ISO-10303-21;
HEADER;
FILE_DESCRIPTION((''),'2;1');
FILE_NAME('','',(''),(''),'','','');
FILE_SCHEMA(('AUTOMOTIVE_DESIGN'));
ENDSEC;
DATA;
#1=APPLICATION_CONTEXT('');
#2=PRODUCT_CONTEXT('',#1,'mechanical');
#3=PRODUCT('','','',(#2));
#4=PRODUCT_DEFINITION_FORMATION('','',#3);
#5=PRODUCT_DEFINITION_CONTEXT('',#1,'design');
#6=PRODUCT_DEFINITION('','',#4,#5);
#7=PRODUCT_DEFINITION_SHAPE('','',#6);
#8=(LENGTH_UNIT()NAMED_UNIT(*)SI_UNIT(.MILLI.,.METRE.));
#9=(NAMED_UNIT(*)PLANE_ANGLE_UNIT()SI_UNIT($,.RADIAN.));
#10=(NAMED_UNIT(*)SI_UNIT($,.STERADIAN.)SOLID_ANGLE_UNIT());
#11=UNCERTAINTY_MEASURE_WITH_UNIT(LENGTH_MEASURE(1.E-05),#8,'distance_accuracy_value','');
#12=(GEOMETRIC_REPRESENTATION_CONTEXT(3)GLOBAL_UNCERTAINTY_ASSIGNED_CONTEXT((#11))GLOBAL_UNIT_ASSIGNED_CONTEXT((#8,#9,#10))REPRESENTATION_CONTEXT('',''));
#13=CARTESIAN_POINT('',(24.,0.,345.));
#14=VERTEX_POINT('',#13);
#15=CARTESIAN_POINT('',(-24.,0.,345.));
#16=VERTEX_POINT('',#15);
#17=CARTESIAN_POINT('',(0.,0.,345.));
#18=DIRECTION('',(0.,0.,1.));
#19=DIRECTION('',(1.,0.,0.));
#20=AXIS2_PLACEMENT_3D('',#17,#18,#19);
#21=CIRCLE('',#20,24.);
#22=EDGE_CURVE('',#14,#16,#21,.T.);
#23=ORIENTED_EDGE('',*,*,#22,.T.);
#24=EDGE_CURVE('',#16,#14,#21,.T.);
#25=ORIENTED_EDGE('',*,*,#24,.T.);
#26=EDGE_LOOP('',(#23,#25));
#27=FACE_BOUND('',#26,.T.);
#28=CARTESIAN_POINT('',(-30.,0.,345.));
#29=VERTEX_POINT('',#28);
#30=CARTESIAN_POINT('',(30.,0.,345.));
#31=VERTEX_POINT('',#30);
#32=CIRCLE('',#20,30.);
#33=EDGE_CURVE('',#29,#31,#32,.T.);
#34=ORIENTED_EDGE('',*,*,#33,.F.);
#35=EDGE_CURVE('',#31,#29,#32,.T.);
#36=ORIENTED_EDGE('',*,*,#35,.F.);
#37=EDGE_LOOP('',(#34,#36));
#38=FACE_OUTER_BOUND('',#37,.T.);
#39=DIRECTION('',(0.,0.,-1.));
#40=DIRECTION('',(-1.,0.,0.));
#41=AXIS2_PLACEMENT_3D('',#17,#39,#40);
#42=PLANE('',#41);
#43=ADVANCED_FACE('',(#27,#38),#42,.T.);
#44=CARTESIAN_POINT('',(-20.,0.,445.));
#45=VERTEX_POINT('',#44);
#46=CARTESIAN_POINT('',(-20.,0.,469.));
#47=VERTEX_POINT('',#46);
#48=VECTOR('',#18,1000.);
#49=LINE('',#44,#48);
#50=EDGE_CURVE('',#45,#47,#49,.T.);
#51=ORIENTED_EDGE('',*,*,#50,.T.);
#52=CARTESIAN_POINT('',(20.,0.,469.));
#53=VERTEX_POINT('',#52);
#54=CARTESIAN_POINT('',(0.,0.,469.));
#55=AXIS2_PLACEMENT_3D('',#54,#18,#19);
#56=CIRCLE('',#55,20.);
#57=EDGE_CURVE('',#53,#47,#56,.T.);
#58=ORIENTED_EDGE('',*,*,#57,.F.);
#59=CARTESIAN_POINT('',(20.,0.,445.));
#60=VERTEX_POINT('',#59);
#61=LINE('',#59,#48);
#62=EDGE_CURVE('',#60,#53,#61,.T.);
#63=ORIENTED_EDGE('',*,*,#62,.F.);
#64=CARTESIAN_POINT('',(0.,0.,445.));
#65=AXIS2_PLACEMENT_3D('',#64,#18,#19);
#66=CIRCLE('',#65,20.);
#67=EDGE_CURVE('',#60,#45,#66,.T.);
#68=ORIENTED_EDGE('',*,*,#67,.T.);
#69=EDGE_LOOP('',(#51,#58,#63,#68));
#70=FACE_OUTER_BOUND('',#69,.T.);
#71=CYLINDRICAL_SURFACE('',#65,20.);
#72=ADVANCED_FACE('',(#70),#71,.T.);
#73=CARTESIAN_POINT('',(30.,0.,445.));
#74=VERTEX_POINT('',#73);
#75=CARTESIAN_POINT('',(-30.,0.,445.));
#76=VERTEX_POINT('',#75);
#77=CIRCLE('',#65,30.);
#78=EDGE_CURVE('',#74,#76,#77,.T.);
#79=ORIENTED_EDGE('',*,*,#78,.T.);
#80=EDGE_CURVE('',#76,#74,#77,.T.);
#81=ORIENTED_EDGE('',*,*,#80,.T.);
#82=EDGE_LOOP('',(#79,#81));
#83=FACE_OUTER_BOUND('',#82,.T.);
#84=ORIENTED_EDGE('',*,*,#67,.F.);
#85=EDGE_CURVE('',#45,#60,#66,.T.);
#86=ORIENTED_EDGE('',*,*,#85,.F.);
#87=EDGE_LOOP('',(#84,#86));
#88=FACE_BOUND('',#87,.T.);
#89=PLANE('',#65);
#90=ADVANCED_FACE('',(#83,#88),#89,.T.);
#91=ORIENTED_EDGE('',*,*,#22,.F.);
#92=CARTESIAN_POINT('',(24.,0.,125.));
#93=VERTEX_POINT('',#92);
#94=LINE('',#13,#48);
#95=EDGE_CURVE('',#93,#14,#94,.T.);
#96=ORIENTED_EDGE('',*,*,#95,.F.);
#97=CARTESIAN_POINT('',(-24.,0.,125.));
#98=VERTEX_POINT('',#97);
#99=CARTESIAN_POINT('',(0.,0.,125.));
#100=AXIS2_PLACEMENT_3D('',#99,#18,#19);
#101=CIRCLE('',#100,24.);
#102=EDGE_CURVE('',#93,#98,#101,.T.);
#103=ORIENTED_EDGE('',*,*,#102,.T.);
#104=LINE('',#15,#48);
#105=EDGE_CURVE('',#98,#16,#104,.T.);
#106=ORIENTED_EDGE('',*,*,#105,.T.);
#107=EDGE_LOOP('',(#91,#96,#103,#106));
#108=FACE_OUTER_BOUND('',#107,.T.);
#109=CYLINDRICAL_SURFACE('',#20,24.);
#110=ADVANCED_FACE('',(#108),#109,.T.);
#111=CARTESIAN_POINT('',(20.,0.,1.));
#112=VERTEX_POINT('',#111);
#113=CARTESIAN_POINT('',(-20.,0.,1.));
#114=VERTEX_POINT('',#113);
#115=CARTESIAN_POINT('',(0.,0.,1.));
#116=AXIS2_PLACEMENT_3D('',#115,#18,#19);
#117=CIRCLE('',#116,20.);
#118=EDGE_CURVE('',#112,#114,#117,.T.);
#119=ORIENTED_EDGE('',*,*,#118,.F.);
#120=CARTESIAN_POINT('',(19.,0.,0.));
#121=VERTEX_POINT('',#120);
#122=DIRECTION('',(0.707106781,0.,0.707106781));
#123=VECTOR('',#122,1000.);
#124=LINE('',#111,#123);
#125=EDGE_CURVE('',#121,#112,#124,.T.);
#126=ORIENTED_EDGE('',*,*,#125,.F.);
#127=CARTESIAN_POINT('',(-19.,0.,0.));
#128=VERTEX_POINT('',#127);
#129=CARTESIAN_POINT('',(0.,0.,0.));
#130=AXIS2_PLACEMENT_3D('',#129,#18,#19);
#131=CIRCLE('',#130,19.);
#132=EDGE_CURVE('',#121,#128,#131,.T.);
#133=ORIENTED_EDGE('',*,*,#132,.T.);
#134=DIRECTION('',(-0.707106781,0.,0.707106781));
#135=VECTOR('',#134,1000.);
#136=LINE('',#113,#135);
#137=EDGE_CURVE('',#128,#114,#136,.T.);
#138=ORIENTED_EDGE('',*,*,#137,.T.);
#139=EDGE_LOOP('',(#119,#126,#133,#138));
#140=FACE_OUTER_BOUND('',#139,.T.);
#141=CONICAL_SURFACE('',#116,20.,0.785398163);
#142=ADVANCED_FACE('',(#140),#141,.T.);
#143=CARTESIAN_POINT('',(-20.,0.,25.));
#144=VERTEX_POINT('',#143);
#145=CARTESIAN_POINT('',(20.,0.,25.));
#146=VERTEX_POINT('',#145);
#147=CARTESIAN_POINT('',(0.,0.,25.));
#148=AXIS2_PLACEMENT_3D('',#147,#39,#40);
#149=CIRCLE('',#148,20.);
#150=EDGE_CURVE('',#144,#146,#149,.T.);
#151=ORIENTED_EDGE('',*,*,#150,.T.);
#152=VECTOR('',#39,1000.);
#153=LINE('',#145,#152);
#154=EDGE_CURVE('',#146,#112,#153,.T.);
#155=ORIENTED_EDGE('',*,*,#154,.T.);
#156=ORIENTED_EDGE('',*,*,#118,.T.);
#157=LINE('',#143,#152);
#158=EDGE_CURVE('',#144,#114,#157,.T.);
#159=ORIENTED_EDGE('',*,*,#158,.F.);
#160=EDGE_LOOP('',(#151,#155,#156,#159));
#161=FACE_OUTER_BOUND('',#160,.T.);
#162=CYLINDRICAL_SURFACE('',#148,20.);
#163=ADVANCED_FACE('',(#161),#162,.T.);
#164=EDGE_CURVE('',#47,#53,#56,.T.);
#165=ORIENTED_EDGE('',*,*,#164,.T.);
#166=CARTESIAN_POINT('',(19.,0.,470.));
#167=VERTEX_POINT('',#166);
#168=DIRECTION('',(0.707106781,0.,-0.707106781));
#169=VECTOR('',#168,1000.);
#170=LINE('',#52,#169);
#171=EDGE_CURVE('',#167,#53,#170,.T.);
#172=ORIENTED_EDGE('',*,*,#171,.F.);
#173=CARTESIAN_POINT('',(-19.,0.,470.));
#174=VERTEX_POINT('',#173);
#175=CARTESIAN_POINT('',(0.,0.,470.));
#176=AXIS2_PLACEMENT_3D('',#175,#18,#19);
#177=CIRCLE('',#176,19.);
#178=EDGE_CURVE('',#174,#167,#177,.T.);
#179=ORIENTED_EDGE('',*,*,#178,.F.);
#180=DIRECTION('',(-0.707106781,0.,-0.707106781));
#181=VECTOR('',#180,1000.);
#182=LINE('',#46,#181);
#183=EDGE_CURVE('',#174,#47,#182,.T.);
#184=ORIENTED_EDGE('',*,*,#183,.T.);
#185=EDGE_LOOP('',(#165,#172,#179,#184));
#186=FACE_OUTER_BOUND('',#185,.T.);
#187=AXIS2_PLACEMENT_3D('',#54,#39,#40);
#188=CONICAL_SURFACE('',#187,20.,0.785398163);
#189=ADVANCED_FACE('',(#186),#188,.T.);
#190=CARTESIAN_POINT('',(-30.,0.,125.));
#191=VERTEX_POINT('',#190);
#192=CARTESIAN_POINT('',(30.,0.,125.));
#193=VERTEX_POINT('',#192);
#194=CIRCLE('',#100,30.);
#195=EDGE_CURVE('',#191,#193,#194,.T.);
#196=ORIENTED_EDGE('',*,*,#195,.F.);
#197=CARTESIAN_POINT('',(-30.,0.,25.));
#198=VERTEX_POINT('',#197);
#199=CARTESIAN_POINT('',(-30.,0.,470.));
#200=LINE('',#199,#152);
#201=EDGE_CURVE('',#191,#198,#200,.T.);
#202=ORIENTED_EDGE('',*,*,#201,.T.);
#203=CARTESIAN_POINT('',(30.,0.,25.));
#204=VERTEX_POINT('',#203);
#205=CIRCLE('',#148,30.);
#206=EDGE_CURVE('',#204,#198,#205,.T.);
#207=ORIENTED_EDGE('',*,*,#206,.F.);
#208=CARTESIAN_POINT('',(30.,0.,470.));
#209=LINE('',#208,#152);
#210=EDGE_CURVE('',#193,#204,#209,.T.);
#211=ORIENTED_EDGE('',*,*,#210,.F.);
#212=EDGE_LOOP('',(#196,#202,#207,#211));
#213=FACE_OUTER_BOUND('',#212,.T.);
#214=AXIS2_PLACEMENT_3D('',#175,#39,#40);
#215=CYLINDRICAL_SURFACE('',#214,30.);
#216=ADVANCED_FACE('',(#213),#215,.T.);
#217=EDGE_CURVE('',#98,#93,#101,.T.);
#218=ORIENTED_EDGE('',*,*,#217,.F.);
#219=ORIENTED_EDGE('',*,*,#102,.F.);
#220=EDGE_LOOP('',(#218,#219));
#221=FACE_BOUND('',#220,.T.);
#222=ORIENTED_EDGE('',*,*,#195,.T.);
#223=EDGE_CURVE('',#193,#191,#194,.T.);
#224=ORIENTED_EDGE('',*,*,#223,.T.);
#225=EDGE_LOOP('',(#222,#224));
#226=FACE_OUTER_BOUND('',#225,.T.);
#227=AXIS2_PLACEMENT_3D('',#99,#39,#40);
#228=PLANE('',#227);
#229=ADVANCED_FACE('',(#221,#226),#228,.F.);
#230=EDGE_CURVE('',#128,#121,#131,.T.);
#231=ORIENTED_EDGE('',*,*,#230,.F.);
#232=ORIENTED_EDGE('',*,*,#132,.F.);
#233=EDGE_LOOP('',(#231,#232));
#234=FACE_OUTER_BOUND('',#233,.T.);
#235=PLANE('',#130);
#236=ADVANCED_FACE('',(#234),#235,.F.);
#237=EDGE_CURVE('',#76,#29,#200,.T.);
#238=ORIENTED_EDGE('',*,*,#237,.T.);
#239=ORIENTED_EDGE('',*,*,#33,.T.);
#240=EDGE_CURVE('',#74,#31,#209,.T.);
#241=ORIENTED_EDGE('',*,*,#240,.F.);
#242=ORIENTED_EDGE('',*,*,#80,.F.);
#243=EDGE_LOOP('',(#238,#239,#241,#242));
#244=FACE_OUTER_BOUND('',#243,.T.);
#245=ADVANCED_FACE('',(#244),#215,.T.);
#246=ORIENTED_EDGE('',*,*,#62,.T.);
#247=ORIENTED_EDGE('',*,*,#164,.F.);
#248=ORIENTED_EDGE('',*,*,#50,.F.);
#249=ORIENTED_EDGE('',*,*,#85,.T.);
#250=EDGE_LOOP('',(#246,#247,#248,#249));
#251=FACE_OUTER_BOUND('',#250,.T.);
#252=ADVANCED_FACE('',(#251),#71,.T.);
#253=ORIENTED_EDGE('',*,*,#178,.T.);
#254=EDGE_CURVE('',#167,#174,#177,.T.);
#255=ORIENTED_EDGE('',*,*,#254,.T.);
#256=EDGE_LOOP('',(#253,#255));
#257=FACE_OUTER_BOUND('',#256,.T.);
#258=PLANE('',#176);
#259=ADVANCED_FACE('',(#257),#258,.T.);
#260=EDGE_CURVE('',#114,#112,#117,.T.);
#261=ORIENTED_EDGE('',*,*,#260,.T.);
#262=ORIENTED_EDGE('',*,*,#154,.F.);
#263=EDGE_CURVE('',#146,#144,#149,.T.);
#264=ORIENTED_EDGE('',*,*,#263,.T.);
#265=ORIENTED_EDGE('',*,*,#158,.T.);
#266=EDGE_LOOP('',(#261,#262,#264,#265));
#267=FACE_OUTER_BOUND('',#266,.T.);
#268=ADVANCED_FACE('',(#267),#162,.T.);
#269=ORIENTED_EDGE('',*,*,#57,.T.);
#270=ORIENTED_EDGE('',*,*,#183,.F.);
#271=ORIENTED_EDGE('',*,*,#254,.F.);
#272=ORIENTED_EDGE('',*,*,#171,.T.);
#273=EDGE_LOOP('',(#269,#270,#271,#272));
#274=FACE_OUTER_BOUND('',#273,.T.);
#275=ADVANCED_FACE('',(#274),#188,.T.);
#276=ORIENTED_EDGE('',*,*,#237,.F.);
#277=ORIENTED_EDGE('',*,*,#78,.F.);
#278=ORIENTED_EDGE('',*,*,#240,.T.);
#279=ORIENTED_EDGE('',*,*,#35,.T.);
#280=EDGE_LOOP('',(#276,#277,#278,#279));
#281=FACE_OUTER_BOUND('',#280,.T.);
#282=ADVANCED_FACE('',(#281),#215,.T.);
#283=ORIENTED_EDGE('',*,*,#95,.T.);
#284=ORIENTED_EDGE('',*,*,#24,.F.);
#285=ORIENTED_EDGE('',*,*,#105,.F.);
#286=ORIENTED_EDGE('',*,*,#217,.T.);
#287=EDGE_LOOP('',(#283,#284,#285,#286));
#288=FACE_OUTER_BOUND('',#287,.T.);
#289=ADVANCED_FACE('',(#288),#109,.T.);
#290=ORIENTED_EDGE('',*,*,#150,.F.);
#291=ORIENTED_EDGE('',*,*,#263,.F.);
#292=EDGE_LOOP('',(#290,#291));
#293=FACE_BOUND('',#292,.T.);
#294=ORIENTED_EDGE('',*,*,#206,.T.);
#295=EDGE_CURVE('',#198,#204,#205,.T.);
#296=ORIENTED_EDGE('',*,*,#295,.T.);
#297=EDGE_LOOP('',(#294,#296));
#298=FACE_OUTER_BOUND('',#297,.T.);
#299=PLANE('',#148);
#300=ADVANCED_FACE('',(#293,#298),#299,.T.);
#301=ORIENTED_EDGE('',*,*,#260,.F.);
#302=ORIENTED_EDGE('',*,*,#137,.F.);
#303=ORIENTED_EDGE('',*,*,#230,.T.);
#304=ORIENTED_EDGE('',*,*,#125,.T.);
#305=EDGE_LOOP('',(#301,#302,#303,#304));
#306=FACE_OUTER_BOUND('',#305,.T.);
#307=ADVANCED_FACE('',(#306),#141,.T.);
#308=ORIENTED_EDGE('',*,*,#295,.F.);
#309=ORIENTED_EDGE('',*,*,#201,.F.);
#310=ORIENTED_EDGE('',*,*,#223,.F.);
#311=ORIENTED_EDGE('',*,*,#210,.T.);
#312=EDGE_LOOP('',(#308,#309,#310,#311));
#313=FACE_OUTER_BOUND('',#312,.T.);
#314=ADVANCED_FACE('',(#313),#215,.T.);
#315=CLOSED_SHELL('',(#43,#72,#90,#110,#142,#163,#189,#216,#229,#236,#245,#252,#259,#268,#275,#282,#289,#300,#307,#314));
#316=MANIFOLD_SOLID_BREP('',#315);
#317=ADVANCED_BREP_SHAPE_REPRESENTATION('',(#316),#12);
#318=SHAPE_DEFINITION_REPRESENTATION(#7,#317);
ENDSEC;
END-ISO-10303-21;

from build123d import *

# Parameters (mm, degrees)
SKETCH_2_R          = 30
EXTRUDE_1_DEPTH     = 470
CUT_EXTRUDE_START   = -25
SKETCH_3_R          = 30
SKETCH_3_R_2        = 20
CUT_EXTRUDE_1_DEPTH = 25
SKETCH_4_R          = 30
SKETCH_4_R_2        = 20
CUT_EXTRUDE_2_DEPTH = 25
SKETCH_5_W          = 6
SKETCH_5_H          = 220


with BuildPart() as part:
    # 草图2 → 凸台-拉伸1 (new body)
    with BuildSketch(Plane.XY):
        with Locations(Location((0, 0, 0), (0, 0, 180))):
            Circle(SKETCH_2_R)
    extrude(amount=EXTRUDE_1_DEPTH)

    # 草图3 → 切除-拉伸1 (cut)
    with BuildSketch(Plane.XY.offset(470).offset(CUT_EXTRUDE_START)):
        with Locations(Location((0, 0, 0), (0, 0, 180))):
            Circle(SKETCH_3_R)
        Circle(SKETCH_3_R_2, mode=Mode.SUBTRACT)
    extrude(amount=CUT_EXTRUDE_1_DEPTH, mode=Mode.SUBTRACT)

    # 草图4 → 切除-拉伸2 (cut)
    with BuildSketch(Plane(origin=(0, 0, 0), x_dir=(-1, 0, 0), z_dir=(0, 0, -1))):
        Circle(SKETCH_4_R)
        with Locations(Location((0, 0, 0), (0, 0, 180))):
            Circle(SKETCH_4_R_2, mode=Mode.SUBTRACT)
    extrude(amount=-CUT_EXTRUDE_2_DEPTH, mode=Mode.SUBTRACT)

    # 草图5 → 切除-旋转1 (revolve, cut)
    with BuildSketch(Plane(origin=(0, 0, 0), x_dir=(1, 0, 0), z_dir=(0, 1, 0))):
        with Locations((-27, -235)):
            Rectangle(SKETCH_5_W, SKETCH_5_H)
    revolve(axis=Axis((0, 0, 345), (0, 0, -1)), mode=Mode.SUBTRACT)

    # 草图6 → 切除-旋转2 (revolve, cut)
    with BuildSketch(Plane(origin=(0, 0, 0), x_dir=(1, 0, 0), z_dir=(0, 1, 0))):
        Polygon((20, -470), (19, -470), (20, -469), align=None)
        Polygon((20, -1), (19, 0), (20, 0), align=None)
    revolve(axis=Axis((0, 0, 470), (0, 0, -1)), mode=Mode.SUBTRACT)


solid = part.part
